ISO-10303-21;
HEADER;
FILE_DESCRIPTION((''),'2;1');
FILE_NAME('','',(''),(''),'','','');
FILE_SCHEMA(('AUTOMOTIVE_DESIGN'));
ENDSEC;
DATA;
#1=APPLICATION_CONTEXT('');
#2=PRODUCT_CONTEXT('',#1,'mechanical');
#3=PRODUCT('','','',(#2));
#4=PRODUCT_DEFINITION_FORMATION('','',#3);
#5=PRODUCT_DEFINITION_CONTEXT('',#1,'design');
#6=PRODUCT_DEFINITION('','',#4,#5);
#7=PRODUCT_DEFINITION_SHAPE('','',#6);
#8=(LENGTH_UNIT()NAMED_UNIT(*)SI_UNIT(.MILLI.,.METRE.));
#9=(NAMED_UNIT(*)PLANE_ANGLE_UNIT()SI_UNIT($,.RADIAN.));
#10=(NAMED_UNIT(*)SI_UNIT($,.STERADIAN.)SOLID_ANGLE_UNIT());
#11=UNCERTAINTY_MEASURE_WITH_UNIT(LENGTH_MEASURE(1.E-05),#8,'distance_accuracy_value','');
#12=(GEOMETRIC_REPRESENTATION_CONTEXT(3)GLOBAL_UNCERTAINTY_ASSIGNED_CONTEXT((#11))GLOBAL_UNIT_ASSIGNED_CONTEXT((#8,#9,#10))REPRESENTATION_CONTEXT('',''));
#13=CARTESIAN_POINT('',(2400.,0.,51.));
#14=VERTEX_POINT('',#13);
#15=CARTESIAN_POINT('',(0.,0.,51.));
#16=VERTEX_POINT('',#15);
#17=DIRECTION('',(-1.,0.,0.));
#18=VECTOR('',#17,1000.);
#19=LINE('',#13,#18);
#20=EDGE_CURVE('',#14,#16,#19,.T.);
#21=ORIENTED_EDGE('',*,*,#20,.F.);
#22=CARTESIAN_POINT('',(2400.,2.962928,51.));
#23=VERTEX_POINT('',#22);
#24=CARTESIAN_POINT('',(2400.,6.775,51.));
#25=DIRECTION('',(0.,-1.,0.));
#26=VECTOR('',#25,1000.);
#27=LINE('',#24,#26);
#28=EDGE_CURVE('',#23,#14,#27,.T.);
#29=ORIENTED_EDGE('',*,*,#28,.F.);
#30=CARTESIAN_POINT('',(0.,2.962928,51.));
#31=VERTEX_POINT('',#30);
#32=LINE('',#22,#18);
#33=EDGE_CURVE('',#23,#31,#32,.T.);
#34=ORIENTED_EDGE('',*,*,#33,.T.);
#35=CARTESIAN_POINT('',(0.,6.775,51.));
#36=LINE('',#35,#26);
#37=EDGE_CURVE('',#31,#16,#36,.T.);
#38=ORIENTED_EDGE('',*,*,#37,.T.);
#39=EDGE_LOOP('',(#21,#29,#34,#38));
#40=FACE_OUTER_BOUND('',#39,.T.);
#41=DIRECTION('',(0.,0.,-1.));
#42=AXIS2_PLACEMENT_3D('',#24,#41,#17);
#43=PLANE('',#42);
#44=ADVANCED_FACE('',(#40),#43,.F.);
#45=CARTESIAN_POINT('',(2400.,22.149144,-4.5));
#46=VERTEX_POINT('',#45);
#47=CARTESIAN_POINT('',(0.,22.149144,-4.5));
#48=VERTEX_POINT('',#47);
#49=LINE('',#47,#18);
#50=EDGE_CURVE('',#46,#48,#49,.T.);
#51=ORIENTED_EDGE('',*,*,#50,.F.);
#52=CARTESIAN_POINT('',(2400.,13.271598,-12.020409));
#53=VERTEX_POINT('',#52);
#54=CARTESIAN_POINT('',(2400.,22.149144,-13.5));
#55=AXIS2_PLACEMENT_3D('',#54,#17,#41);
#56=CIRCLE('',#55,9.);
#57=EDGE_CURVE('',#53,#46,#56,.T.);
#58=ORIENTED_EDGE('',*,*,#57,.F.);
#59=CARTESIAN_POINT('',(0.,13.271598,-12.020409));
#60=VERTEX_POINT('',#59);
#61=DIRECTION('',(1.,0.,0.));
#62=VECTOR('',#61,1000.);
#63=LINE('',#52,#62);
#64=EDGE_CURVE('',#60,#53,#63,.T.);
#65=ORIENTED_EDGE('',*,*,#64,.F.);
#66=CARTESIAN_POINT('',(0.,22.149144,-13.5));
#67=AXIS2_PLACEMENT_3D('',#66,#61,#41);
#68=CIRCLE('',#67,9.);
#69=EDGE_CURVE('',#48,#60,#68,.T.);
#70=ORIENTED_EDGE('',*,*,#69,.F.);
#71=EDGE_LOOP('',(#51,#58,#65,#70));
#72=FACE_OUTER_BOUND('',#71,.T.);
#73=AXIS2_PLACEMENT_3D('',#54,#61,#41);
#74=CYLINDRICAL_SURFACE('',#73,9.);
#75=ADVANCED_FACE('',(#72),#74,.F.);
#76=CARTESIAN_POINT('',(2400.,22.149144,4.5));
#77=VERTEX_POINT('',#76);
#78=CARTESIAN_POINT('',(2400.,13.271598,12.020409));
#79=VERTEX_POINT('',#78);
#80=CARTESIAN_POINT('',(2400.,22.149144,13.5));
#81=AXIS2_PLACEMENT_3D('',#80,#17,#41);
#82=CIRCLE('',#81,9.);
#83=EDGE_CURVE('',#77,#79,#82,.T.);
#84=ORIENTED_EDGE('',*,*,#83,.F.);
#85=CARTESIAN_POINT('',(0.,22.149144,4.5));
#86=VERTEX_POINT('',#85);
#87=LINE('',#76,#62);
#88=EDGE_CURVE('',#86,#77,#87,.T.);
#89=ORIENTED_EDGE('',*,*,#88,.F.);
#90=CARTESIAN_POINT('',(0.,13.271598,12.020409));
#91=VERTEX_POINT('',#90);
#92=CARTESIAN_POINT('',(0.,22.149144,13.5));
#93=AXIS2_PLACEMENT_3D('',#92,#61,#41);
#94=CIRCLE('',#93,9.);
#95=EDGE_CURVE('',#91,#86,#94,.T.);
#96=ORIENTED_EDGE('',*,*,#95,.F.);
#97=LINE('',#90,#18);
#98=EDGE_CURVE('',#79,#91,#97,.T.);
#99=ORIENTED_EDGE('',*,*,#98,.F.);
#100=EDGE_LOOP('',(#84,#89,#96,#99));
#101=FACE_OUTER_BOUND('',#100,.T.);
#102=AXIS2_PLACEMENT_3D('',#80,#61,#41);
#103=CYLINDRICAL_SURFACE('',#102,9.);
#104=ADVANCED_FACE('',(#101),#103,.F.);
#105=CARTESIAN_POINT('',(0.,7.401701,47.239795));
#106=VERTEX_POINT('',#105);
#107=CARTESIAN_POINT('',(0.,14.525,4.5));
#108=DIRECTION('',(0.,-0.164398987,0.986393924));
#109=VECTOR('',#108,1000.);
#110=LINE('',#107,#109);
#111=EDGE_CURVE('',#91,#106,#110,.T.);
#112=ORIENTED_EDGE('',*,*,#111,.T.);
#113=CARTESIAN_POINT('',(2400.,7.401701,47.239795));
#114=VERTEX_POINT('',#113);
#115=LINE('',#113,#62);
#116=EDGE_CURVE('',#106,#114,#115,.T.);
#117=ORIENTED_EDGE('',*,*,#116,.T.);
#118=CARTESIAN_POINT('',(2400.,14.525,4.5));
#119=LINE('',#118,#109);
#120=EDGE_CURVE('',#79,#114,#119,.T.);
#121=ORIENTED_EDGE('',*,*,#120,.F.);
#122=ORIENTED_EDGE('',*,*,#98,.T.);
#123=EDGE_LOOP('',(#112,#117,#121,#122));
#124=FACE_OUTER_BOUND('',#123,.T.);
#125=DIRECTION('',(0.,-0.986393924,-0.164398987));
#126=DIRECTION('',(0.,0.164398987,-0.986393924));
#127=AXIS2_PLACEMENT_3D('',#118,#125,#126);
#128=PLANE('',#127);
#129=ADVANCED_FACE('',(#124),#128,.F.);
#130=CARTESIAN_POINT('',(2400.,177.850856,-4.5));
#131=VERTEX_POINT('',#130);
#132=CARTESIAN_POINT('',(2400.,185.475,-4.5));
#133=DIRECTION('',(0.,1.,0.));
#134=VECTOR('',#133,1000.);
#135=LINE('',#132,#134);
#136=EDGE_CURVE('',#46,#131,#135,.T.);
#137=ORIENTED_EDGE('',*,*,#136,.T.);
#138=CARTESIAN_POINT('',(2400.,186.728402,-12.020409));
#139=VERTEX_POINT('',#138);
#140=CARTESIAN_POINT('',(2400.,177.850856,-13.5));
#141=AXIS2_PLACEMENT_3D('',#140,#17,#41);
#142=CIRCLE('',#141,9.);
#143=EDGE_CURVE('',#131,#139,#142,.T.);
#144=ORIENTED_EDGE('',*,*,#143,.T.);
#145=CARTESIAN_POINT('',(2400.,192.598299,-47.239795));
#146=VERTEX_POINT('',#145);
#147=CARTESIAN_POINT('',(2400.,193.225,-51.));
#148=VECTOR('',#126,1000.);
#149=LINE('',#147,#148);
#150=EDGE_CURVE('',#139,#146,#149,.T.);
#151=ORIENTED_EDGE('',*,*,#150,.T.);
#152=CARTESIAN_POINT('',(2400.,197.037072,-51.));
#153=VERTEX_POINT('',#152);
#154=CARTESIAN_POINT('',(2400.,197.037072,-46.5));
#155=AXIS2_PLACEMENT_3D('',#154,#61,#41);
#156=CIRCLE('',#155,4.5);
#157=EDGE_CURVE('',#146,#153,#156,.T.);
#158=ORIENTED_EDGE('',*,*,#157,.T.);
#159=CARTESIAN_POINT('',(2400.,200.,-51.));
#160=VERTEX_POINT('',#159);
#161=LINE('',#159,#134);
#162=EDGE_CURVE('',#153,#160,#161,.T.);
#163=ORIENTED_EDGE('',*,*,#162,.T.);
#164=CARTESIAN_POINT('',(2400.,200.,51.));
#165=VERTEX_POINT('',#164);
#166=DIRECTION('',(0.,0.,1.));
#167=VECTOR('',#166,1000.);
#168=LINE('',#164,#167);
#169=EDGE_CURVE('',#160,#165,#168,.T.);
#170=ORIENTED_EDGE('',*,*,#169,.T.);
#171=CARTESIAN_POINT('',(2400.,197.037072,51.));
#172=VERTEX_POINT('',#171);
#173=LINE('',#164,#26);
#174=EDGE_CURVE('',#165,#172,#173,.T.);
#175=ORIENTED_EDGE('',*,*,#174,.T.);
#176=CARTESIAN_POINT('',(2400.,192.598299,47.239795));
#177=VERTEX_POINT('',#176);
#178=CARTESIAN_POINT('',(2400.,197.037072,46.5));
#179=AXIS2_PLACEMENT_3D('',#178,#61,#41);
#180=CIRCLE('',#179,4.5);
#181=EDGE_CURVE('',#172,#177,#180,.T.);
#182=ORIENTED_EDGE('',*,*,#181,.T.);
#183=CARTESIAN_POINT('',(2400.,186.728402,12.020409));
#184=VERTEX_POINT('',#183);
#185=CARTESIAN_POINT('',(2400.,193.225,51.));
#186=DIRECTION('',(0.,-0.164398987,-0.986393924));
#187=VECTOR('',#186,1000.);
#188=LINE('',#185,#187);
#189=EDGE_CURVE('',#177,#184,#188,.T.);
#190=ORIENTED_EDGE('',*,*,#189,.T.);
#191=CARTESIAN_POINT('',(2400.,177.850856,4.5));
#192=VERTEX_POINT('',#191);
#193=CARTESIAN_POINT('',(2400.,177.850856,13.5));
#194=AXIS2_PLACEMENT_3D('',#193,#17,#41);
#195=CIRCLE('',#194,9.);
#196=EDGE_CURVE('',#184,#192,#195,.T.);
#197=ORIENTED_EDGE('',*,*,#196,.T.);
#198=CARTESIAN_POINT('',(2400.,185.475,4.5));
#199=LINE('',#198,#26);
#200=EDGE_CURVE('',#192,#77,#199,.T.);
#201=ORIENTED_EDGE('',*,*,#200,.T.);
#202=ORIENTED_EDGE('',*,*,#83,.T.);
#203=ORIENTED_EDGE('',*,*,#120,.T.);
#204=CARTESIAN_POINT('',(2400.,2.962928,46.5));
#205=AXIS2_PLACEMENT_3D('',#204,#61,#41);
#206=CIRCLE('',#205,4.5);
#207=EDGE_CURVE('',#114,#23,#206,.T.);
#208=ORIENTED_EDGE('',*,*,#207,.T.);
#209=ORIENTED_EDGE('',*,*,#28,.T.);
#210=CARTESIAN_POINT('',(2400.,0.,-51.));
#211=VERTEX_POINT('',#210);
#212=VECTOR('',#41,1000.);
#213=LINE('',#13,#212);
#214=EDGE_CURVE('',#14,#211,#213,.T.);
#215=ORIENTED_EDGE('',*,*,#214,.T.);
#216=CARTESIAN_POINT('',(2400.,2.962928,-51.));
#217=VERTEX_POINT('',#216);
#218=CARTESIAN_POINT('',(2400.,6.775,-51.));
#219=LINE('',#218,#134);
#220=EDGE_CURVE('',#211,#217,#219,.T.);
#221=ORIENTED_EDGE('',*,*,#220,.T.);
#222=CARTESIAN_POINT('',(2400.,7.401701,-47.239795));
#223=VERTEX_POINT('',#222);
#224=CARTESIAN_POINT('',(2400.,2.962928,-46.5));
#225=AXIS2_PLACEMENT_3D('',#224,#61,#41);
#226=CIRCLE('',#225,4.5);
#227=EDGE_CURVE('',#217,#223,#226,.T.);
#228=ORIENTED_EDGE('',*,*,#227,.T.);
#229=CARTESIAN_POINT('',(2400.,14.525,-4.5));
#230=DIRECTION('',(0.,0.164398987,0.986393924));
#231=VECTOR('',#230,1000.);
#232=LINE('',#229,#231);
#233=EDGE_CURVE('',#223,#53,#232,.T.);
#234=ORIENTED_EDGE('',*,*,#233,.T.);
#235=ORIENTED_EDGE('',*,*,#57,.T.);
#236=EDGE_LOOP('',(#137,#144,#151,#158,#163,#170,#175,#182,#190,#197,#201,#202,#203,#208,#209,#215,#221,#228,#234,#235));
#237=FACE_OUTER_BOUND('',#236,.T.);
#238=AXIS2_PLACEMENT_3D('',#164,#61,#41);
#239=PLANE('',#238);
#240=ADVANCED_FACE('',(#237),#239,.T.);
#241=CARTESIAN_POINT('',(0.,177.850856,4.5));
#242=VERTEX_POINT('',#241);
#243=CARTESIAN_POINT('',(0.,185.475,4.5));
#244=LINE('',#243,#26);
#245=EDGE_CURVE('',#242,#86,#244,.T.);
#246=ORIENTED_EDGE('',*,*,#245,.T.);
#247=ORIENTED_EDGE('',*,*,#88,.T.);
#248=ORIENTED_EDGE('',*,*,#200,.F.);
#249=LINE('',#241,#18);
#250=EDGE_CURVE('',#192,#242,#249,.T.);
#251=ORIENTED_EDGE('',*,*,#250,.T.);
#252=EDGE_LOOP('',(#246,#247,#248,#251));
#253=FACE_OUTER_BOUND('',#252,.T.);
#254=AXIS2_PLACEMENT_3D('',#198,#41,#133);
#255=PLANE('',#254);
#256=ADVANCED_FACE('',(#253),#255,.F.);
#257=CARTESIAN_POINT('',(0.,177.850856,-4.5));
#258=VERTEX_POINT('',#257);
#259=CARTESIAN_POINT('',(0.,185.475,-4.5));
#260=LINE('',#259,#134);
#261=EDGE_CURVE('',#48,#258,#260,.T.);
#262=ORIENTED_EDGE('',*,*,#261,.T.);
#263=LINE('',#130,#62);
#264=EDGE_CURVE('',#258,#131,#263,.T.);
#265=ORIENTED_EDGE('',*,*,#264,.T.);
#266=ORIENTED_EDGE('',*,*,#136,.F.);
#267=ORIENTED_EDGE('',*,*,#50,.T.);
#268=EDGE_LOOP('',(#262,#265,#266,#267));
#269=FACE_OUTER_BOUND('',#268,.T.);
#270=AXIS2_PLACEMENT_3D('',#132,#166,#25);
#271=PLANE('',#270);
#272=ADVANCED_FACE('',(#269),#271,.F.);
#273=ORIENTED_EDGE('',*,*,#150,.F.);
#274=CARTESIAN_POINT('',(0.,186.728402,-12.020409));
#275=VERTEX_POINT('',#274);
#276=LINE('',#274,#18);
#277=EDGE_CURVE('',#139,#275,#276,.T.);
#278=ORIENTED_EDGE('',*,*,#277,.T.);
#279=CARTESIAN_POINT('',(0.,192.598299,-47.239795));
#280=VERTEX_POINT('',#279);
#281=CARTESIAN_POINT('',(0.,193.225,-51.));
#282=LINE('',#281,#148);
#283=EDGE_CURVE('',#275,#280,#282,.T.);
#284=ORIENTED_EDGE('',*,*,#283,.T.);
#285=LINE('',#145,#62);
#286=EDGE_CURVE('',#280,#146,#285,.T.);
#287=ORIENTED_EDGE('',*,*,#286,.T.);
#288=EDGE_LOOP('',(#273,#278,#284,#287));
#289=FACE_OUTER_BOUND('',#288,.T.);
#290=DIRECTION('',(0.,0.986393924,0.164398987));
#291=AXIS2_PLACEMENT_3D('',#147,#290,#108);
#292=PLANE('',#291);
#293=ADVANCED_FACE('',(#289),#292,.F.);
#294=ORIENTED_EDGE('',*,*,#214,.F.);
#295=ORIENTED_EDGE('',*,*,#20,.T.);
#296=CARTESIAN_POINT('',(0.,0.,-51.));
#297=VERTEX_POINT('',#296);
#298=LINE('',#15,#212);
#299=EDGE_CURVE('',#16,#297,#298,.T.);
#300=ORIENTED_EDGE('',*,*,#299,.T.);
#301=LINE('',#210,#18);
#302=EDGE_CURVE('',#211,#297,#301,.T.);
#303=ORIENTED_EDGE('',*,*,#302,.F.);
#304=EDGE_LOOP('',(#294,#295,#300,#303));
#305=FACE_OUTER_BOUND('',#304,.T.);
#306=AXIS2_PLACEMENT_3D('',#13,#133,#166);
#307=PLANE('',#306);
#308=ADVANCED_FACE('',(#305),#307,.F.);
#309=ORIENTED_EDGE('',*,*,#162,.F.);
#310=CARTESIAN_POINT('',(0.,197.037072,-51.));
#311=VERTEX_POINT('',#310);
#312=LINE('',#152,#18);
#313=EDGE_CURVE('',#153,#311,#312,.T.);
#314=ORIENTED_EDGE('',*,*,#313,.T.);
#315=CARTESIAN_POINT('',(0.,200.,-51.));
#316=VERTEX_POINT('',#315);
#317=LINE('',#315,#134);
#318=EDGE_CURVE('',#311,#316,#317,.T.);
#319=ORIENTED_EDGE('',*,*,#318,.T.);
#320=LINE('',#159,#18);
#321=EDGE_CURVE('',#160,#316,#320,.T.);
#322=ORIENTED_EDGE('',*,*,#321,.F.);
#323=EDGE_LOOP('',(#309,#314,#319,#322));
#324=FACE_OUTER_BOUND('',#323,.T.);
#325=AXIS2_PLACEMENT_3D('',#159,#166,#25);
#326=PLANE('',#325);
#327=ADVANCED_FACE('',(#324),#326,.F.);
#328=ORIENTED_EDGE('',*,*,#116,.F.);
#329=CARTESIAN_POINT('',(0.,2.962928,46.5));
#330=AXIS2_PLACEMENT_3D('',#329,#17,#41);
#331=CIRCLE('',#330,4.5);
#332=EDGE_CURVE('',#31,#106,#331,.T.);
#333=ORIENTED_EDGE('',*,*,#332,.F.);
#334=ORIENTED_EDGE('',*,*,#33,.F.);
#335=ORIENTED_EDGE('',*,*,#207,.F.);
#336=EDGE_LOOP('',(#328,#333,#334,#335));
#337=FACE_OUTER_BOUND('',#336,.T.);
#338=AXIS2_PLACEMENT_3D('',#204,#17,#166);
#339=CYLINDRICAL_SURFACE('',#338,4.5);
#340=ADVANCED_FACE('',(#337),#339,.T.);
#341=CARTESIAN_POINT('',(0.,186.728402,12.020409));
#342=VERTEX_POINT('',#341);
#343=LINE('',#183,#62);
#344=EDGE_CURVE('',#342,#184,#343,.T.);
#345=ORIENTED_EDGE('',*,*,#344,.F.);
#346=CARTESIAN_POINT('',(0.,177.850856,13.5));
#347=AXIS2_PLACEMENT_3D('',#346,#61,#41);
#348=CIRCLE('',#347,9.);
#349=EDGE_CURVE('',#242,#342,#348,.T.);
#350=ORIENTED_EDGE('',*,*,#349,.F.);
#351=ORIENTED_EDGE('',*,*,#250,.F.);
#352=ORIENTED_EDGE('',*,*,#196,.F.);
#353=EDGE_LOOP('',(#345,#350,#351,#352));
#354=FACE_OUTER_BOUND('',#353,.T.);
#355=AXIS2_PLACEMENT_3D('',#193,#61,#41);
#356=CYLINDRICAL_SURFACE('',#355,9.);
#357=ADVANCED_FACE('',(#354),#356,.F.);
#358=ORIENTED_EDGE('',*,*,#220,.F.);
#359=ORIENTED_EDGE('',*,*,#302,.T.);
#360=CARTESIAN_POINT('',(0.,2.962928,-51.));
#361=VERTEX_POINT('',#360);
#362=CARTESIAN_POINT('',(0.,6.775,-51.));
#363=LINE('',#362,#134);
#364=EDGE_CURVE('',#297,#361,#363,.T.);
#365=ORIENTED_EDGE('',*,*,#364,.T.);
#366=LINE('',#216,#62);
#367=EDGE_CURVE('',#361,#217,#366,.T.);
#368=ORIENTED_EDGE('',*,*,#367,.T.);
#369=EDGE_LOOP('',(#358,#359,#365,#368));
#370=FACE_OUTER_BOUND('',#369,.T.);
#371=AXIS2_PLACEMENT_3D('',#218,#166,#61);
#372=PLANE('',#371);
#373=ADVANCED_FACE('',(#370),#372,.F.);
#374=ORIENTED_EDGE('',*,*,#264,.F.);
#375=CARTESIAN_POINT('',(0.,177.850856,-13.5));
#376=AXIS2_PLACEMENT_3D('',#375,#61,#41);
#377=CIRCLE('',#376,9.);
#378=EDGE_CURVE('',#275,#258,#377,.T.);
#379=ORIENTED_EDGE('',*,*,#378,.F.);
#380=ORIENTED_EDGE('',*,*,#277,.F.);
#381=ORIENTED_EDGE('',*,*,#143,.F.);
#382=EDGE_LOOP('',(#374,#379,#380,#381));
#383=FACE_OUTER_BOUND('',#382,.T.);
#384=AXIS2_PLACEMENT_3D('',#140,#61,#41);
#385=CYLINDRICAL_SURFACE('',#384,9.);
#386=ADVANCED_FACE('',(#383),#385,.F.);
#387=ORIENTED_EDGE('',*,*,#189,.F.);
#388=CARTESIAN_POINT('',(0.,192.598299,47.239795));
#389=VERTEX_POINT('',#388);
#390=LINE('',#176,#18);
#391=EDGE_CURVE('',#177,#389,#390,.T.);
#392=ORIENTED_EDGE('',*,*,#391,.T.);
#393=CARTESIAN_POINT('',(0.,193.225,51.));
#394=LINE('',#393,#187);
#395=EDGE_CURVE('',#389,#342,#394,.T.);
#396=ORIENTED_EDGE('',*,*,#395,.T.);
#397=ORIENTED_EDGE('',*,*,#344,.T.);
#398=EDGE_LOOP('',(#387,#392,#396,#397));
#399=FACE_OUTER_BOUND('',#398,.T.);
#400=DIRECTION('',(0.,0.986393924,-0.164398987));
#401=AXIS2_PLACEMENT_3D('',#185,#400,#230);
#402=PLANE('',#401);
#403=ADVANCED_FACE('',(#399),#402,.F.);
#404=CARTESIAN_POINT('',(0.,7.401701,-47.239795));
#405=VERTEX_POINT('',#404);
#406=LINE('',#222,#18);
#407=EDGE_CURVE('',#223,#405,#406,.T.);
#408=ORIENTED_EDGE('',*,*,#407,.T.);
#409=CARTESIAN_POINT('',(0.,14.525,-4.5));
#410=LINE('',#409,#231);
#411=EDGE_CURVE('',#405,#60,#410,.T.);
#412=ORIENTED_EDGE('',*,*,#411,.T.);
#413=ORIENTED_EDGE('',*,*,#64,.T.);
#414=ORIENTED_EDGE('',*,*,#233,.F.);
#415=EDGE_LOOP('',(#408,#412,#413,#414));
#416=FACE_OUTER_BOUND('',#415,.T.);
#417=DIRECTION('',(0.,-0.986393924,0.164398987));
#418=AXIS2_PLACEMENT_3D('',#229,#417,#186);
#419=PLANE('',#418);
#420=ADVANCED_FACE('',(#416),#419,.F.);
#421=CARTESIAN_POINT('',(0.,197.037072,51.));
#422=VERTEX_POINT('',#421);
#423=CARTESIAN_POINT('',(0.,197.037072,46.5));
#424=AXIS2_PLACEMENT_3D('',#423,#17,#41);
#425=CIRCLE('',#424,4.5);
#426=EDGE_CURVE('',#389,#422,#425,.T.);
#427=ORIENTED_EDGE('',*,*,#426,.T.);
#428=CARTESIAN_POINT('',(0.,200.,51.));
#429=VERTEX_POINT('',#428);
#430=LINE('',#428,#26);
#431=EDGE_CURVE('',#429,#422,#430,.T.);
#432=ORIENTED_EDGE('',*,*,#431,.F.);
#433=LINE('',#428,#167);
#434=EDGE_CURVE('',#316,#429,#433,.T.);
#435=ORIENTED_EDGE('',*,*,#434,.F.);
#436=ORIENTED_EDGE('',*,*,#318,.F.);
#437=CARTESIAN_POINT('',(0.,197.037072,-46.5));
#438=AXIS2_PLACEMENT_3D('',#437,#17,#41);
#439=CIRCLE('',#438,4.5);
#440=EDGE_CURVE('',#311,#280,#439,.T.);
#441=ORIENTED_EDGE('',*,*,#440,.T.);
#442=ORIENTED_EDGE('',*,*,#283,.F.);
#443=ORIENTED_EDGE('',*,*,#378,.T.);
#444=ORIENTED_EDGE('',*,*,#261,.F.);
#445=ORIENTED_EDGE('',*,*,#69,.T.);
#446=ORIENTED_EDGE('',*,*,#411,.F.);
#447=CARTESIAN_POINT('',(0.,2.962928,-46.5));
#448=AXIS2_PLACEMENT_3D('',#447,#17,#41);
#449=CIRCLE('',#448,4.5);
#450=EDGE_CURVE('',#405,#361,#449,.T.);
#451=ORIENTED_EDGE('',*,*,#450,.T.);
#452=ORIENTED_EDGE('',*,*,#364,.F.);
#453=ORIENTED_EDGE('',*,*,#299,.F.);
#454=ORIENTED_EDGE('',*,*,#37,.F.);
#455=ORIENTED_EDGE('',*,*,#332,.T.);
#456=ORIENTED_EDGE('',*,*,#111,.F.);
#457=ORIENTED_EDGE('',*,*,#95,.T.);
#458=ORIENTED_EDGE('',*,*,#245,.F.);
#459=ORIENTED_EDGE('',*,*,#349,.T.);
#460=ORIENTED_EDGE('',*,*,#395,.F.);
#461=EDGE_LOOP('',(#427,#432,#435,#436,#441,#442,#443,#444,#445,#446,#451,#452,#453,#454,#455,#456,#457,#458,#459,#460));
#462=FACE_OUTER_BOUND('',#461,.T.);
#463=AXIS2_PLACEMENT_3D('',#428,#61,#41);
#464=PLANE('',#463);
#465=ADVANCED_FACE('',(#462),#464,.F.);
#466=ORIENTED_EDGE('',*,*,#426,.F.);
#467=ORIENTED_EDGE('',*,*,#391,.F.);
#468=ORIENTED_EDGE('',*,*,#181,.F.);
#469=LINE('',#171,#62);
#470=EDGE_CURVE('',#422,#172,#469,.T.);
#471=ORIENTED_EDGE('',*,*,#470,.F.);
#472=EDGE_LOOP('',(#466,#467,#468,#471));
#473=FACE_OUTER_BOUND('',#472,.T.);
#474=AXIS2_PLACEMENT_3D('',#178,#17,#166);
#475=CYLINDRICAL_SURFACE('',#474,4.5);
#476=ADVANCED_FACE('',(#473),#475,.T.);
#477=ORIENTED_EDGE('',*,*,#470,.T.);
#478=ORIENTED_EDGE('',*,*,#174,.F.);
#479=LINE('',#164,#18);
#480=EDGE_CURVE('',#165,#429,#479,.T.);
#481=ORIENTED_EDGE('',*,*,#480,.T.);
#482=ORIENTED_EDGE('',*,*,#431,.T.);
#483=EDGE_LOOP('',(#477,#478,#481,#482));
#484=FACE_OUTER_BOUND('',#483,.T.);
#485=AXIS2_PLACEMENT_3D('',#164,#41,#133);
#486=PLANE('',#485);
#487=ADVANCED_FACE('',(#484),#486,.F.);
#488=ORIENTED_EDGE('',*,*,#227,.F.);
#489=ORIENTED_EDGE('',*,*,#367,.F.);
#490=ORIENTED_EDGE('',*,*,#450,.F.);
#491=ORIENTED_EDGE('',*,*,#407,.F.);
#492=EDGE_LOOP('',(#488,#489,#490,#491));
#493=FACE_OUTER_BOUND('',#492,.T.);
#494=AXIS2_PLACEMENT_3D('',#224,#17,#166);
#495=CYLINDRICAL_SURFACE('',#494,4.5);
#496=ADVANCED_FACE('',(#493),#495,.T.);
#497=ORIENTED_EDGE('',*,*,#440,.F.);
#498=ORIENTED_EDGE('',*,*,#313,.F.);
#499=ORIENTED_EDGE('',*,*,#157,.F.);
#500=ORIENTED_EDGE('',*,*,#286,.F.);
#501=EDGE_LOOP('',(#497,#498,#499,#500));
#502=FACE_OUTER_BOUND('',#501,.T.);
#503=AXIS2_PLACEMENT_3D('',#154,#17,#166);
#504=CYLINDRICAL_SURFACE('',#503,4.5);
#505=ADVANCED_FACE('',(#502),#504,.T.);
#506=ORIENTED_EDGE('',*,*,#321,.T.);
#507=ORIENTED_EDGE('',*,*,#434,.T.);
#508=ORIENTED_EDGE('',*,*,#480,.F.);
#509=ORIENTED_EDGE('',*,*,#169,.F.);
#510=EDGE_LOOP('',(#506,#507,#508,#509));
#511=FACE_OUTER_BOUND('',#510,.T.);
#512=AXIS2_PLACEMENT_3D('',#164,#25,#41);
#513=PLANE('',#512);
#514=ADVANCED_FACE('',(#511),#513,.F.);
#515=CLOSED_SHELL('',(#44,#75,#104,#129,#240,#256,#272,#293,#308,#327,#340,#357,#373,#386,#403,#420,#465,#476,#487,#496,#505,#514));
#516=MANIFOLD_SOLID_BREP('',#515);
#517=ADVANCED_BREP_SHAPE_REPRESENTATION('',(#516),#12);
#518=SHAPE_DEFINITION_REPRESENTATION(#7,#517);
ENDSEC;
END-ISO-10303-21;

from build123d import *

# Parameters (mm, degrees)
BASE_DEPTH = 2400
FILLET1_R  = 9
FILLET2_R  = 4.5


with BuildPart() as part:
    # Sketch1 → Base (new body)
    with BuildSketch(Plane(origin=(0, 0, 0), x_dir=(0, 0, -1), z_dir=(1, 0, 0))):
        Polygon((-51, 0), (51, 0), (51, 6.775), (4.5, 14.525), (4.5, 185.475), (51, 193.225), (51, 200), (-51, 200), (-51, 193.225), (-4.5, 185.475), (-4.5, 14.525), (-51, 6.775), align=None)
    extrude(amount=BASE_DEPTH)

    # Fillet1
    fillet1_edges = [part.edges().sort_by_distance(p)[0] for p in [
        (1200, 14.525, 4.5),
        (1200, 185.475, 4.5),
        (1200, 185.475, -4.5),
        (1200, 14.525, -4.5),
    ]]
    fillet(fillet1_edges, radius=FILLET1_R)

    # Fillet2
    fillet2_edges = [part.edges().sort_by_distance(p)[0] for p in [
        (1200, 6.775, 51),
        (1200, 193.225, 51),
        (1200, 193.225, -51),
        (1200, 6.775, -51),
    ]]
    fillet(fillet2_edges, radius=FILLET2_R)


solid = part.part
